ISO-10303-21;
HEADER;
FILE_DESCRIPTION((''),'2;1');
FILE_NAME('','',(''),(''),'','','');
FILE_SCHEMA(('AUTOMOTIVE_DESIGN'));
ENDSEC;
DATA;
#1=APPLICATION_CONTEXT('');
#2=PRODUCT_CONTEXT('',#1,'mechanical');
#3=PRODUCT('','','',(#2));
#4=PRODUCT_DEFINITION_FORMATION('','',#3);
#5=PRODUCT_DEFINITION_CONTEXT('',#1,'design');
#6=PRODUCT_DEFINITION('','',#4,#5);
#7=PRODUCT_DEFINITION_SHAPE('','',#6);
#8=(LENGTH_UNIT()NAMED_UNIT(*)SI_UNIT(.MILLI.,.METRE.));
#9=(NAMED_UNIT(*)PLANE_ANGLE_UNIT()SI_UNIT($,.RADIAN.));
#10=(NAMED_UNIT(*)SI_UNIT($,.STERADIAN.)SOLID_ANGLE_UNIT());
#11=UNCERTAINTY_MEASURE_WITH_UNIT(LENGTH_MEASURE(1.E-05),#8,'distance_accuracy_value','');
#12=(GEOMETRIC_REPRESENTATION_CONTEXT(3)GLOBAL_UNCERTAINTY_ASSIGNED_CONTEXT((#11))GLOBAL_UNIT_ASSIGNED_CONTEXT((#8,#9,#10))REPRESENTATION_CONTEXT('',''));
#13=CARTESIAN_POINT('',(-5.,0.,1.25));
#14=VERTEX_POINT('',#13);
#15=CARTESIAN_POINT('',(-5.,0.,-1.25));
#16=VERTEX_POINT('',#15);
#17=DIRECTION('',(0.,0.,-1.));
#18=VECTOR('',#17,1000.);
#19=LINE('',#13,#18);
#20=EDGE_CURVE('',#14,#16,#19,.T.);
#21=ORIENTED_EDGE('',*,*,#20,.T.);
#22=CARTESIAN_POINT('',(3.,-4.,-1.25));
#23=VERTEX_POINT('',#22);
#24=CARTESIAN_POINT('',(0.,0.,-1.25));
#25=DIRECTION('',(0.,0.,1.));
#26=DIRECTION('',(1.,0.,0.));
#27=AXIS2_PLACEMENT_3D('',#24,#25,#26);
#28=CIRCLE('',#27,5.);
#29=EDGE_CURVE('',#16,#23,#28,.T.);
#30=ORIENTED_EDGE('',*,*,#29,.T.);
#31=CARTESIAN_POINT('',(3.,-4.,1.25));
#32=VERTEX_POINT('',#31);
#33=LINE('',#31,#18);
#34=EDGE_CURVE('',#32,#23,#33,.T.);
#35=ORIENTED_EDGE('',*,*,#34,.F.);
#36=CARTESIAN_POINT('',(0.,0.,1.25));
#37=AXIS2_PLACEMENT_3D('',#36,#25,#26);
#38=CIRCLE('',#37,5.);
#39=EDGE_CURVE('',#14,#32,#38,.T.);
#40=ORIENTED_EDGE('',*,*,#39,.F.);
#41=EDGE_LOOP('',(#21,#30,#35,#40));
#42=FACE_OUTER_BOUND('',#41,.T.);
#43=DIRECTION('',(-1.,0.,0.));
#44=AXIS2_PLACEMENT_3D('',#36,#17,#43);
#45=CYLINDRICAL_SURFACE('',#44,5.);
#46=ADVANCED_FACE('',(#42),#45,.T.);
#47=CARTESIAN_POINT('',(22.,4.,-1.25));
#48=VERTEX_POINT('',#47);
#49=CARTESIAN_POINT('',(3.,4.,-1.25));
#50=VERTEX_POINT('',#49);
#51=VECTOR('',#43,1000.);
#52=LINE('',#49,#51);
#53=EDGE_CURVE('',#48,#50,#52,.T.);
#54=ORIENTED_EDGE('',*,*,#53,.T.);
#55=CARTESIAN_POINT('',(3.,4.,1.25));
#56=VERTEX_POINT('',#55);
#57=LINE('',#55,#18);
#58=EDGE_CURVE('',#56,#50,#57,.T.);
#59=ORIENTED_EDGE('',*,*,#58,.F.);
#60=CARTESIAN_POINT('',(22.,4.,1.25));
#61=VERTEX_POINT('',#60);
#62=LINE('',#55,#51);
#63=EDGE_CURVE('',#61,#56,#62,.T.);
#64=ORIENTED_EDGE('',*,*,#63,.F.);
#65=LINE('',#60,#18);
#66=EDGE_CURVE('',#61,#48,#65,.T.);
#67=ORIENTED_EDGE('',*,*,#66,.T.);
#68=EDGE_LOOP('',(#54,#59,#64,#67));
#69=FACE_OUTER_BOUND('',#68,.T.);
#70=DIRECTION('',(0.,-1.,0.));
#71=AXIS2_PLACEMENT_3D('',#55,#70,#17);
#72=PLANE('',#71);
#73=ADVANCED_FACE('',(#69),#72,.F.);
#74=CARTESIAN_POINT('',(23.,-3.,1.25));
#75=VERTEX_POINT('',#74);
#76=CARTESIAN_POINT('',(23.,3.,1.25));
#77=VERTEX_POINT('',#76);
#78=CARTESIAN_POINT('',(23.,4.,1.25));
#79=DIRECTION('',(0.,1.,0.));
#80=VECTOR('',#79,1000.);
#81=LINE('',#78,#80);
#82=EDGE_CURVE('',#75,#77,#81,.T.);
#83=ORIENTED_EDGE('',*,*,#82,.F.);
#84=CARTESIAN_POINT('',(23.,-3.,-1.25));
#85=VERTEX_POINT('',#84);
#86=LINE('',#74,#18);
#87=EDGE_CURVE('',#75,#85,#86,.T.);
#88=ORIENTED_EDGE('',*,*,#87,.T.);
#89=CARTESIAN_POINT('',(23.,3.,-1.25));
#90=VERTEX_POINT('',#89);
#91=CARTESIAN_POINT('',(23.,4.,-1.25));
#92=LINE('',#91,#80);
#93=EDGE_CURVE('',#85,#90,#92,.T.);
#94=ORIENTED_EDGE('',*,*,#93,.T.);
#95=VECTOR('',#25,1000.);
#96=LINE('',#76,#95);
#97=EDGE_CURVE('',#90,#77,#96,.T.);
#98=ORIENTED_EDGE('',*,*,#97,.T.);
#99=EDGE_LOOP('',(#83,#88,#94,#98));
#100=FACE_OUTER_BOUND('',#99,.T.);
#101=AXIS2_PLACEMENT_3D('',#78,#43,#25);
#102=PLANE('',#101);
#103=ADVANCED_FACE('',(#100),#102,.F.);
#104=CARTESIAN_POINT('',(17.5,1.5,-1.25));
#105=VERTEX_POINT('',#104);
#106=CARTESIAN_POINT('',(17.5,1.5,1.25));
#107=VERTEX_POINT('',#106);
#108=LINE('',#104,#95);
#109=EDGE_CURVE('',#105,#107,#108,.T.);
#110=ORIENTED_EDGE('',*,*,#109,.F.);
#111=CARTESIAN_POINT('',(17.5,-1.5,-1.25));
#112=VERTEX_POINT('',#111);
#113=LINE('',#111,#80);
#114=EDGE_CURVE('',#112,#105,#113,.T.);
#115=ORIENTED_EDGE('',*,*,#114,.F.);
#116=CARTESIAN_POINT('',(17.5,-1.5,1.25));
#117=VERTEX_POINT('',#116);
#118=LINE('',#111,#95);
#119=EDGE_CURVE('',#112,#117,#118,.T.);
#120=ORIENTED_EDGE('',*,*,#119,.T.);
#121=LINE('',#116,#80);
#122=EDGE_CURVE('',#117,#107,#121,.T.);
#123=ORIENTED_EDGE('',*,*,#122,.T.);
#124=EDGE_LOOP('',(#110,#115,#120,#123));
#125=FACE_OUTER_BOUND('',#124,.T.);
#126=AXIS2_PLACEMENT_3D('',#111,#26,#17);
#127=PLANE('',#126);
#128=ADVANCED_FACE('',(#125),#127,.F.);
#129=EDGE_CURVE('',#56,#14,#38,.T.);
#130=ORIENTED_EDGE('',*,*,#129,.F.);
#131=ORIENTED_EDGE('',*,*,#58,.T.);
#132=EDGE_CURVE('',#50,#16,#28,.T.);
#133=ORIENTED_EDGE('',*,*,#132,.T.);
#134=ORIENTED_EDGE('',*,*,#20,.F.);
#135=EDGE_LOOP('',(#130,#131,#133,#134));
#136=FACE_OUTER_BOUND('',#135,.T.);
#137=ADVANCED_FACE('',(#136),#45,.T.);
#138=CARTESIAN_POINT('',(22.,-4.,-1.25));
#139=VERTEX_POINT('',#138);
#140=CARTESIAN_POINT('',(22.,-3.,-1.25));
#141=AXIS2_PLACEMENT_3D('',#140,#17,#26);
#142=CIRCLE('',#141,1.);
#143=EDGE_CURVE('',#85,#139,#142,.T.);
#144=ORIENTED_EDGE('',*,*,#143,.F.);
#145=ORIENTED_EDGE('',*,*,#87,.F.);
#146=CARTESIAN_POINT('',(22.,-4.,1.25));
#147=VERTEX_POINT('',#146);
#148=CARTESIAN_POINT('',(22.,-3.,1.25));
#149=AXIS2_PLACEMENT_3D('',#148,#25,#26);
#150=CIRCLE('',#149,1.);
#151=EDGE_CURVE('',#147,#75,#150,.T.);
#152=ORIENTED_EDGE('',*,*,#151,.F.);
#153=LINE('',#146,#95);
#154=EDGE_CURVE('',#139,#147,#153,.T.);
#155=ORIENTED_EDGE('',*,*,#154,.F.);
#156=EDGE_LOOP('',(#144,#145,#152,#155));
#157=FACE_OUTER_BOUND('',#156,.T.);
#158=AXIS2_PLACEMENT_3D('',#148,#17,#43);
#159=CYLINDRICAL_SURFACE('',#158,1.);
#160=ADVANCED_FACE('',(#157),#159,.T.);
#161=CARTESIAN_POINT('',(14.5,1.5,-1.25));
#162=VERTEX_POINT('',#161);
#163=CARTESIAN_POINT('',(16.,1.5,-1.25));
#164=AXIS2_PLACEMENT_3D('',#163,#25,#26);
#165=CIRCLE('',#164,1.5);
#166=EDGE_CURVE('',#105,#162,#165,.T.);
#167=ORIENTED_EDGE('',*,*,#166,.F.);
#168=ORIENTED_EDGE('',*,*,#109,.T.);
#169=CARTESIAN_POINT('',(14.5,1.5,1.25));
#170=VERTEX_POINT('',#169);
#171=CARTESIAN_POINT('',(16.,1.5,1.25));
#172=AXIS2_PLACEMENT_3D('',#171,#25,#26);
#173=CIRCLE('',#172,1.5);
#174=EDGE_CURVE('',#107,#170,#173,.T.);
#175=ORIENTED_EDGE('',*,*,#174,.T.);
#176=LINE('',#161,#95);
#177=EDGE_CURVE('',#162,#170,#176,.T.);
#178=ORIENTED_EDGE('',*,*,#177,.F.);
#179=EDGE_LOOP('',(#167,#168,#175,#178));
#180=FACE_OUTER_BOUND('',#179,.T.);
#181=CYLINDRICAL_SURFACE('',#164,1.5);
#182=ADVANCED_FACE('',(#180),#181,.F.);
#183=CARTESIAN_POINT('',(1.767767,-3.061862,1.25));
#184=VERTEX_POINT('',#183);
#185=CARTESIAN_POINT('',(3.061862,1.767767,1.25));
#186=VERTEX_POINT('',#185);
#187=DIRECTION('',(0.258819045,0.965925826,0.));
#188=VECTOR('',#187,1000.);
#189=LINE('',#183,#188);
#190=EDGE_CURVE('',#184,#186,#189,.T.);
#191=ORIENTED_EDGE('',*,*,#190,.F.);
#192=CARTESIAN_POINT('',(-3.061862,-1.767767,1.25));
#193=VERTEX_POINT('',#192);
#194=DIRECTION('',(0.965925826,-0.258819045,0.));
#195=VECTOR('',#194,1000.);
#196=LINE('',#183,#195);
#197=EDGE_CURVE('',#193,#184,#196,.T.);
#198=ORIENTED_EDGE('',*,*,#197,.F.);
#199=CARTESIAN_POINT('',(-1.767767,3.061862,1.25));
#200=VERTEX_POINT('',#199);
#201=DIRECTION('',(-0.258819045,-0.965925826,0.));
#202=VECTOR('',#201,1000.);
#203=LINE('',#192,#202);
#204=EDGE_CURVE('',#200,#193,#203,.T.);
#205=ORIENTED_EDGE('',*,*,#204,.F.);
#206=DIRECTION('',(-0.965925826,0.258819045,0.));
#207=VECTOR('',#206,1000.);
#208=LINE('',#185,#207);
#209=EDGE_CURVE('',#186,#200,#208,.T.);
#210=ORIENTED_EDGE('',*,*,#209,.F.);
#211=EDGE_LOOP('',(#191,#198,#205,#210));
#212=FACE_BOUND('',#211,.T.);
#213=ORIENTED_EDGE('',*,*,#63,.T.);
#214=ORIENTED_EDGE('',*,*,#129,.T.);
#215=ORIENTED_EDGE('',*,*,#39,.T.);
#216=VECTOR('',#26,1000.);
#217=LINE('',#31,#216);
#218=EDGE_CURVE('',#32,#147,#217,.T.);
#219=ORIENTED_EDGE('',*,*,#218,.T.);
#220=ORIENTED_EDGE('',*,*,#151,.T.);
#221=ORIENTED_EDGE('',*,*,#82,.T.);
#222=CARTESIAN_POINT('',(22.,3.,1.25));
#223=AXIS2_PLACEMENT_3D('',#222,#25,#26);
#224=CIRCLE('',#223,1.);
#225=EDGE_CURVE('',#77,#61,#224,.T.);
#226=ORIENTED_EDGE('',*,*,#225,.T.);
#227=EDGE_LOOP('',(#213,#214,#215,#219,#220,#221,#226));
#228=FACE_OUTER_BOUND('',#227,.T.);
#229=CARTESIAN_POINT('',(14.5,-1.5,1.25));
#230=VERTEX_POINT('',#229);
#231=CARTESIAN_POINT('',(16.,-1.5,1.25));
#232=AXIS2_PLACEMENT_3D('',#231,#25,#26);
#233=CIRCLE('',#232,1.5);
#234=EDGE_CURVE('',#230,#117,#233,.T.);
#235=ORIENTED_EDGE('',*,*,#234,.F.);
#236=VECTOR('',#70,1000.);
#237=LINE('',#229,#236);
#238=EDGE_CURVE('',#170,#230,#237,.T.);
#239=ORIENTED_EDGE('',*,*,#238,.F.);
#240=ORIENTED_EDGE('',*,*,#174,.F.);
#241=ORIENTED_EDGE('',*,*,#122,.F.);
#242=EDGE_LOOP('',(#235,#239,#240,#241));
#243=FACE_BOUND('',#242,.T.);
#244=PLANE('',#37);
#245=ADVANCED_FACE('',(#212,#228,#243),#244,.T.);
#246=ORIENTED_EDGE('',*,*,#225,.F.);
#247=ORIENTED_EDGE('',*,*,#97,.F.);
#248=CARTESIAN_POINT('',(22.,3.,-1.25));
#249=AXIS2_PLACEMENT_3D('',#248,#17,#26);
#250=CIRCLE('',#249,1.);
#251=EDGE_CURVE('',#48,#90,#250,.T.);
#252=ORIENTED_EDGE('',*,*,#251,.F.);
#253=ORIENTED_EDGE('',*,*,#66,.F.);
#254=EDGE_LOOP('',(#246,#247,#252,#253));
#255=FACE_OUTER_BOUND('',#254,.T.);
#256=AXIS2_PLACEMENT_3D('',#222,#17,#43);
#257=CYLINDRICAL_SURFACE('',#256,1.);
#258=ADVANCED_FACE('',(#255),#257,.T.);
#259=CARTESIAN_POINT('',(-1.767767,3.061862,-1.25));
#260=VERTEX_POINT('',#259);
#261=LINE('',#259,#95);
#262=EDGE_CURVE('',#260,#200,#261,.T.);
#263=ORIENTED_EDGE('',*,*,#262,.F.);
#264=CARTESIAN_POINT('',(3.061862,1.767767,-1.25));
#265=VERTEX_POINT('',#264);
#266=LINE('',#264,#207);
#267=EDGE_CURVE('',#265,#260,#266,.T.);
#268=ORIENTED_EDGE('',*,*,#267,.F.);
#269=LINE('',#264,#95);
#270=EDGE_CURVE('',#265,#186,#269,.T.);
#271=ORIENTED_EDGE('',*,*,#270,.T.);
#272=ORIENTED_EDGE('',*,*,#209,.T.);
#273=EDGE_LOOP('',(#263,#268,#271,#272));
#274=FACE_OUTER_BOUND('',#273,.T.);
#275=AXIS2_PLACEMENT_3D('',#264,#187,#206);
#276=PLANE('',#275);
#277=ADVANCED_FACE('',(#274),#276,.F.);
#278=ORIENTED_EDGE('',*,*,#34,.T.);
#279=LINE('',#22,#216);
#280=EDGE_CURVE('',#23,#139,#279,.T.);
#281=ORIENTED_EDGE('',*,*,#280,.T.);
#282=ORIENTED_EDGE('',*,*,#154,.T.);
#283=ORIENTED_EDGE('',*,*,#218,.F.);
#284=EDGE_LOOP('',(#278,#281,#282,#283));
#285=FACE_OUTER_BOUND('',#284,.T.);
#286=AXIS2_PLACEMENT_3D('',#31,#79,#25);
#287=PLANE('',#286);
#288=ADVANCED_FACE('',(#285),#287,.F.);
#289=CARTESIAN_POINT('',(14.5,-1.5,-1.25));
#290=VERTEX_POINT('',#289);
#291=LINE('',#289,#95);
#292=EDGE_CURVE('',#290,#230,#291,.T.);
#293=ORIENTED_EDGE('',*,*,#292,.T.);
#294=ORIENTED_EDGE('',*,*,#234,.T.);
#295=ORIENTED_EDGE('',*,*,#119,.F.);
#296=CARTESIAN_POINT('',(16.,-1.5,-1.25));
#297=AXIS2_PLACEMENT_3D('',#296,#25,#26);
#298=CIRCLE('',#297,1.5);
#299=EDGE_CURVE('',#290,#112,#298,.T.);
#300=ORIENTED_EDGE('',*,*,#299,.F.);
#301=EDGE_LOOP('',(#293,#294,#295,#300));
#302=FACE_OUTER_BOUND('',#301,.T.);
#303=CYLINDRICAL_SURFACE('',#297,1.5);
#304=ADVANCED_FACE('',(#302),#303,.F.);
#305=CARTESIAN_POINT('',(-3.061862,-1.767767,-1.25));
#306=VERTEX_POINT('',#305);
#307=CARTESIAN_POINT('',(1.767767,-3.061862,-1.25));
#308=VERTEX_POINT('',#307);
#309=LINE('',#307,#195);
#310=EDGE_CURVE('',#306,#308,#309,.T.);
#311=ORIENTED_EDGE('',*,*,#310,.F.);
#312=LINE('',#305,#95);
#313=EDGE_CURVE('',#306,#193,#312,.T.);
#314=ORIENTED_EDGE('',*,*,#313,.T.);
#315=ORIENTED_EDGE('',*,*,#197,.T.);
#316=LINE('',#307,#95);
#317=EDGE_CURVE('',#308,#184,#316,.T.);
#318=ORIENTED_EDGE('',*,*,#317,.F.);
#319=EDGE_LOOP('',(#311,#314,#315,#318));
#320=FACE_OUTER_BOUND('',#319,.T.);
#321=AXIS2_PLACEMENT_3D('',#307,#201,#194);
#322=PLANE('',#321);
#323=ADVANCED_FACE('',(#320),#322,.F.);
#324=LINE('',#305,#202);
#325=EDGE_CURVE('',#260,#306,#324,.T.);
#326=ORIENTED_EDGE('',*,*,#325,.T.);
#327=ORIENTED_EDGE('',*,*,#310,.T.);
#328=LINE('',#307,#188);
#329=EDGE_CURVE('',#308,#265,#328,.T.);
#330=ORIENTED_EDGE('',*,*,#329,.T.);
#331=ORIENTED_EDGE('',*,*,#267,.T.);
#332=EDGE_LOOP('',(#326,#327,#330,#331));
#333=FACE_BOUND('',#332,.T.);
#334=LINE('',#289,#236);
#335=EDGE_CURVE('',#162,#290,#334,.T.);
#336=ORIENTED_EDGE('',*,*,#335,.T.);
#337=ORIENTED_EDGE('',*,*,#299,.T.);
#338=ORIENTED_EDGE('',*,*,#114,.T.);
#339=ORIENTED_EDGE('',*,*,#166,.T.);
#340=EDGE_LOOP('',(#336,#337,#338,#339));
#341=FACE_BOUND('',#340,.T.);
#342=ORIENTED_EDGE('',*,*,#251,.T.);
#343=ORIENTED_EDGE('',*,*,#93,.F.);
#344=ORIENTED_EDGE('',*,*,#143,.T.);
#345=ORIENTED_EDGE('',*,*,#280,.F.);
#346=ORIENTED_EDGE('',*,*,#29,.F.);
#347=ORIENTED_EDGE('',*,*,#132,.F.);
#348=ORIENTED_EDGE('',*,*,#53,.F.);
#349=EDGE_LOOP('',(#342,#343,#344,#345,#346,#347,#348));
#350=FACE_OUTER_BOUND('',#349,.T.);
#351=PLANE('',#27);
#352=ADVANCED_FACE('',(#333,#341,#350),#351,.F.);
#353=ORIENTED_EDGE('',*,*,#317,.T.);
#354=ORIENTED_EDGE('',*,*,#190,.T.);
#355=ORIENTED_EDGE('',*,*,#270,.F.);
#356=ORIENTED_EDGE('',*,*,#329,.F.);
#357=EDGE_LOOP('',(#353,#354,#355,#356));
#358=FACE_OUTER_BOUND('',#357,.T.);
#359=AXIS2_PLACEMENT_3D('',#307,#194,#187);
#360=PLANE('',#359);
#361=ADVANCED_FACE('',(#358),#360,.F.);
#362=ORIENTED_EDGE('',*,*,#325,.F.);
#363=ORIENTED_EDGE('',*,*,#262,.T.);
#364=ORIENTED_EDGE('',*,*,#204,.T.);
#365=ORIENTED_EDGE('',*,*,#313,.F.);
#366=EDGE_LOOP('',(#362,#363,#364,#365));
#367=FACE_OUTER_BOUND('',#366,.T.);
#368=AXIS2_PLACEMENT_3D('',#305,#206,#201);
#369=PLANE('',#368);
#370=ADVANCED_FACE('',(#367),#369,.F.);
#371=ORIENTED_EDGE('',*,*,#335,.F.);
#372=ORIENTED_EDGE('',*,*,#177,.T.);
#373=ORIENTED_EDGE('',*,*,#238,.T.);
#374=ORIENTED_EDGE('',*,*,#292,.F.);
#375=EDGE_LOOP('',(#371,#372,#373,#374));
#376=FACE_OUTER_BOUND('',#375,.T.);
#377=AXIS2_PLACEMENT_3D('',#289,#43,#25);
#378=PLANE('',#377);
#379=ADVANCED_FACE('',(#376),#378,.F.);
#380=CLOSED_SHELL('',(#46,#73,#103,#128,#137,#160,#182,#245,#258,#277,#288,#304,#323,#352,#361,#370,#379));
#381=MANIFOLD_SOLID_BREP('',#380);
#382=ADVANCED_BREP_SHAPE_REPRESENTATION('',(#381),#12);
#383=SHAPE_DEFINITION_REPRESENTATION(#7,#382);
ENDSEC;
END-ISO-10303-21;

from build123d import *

# Parameters (mm, degrees)
EXTRUDE_1_DEPTH     = 1.25
CUT_EXTRUDE_1_DEPTH = 24.669600757
FILLET_1_R          = 1


with BuildPart() as part:
    # 草图1 → 凸台-拉伸1 (new, symmetric)
    with BuildSketch(Plane.XY):
        with BuildLine():
            Line((3, 4), (23, 4))
            Line((23, 4), (23, -4))
            Line((23, -4), (3, -4))
            ThreePointArc((3, -4), (-5, 0), (3, 4))
        make_face()
    extrude(amount=EXTRUDE_1_DEPTH, both=True)

    # 草图2 → 切除-拉伸1 (cut, through all)
    with BuildSketch(Plane.XY.offset(1.25)):
        Polygon((1.767766953, -3.061862178), (3.061862178, 1.767766953), (-1.767766953, 3.061862178), (-3.061862178, -1.767766953), align=None)
        with BuildLine():
            Line((14.5, -1.5), (14.5, 1.5))
            ThreePointArc((14.5, 1.5), (16, 3), (17.5, 1.5))
            Line((17.5, 1.5), (17.5, -1.5))
            ThreePointArc((17.5, -1.5), (16, -3), (14.5, -1.5))
        make_face()
    extrude(amount=-CUT_EXTRUDE_1_DEPTH, mode=Mode.SUBTRACT)

    # 圆角1
    fillet_1_edges = [part.edges().sort_by_distance(p)[0] for p in [
        (23, 4, 0),
        (23, -4, 0),
    ]]
    fillet(fillet_1_edges, radius=FILLET_1_R)


solid = part.part
